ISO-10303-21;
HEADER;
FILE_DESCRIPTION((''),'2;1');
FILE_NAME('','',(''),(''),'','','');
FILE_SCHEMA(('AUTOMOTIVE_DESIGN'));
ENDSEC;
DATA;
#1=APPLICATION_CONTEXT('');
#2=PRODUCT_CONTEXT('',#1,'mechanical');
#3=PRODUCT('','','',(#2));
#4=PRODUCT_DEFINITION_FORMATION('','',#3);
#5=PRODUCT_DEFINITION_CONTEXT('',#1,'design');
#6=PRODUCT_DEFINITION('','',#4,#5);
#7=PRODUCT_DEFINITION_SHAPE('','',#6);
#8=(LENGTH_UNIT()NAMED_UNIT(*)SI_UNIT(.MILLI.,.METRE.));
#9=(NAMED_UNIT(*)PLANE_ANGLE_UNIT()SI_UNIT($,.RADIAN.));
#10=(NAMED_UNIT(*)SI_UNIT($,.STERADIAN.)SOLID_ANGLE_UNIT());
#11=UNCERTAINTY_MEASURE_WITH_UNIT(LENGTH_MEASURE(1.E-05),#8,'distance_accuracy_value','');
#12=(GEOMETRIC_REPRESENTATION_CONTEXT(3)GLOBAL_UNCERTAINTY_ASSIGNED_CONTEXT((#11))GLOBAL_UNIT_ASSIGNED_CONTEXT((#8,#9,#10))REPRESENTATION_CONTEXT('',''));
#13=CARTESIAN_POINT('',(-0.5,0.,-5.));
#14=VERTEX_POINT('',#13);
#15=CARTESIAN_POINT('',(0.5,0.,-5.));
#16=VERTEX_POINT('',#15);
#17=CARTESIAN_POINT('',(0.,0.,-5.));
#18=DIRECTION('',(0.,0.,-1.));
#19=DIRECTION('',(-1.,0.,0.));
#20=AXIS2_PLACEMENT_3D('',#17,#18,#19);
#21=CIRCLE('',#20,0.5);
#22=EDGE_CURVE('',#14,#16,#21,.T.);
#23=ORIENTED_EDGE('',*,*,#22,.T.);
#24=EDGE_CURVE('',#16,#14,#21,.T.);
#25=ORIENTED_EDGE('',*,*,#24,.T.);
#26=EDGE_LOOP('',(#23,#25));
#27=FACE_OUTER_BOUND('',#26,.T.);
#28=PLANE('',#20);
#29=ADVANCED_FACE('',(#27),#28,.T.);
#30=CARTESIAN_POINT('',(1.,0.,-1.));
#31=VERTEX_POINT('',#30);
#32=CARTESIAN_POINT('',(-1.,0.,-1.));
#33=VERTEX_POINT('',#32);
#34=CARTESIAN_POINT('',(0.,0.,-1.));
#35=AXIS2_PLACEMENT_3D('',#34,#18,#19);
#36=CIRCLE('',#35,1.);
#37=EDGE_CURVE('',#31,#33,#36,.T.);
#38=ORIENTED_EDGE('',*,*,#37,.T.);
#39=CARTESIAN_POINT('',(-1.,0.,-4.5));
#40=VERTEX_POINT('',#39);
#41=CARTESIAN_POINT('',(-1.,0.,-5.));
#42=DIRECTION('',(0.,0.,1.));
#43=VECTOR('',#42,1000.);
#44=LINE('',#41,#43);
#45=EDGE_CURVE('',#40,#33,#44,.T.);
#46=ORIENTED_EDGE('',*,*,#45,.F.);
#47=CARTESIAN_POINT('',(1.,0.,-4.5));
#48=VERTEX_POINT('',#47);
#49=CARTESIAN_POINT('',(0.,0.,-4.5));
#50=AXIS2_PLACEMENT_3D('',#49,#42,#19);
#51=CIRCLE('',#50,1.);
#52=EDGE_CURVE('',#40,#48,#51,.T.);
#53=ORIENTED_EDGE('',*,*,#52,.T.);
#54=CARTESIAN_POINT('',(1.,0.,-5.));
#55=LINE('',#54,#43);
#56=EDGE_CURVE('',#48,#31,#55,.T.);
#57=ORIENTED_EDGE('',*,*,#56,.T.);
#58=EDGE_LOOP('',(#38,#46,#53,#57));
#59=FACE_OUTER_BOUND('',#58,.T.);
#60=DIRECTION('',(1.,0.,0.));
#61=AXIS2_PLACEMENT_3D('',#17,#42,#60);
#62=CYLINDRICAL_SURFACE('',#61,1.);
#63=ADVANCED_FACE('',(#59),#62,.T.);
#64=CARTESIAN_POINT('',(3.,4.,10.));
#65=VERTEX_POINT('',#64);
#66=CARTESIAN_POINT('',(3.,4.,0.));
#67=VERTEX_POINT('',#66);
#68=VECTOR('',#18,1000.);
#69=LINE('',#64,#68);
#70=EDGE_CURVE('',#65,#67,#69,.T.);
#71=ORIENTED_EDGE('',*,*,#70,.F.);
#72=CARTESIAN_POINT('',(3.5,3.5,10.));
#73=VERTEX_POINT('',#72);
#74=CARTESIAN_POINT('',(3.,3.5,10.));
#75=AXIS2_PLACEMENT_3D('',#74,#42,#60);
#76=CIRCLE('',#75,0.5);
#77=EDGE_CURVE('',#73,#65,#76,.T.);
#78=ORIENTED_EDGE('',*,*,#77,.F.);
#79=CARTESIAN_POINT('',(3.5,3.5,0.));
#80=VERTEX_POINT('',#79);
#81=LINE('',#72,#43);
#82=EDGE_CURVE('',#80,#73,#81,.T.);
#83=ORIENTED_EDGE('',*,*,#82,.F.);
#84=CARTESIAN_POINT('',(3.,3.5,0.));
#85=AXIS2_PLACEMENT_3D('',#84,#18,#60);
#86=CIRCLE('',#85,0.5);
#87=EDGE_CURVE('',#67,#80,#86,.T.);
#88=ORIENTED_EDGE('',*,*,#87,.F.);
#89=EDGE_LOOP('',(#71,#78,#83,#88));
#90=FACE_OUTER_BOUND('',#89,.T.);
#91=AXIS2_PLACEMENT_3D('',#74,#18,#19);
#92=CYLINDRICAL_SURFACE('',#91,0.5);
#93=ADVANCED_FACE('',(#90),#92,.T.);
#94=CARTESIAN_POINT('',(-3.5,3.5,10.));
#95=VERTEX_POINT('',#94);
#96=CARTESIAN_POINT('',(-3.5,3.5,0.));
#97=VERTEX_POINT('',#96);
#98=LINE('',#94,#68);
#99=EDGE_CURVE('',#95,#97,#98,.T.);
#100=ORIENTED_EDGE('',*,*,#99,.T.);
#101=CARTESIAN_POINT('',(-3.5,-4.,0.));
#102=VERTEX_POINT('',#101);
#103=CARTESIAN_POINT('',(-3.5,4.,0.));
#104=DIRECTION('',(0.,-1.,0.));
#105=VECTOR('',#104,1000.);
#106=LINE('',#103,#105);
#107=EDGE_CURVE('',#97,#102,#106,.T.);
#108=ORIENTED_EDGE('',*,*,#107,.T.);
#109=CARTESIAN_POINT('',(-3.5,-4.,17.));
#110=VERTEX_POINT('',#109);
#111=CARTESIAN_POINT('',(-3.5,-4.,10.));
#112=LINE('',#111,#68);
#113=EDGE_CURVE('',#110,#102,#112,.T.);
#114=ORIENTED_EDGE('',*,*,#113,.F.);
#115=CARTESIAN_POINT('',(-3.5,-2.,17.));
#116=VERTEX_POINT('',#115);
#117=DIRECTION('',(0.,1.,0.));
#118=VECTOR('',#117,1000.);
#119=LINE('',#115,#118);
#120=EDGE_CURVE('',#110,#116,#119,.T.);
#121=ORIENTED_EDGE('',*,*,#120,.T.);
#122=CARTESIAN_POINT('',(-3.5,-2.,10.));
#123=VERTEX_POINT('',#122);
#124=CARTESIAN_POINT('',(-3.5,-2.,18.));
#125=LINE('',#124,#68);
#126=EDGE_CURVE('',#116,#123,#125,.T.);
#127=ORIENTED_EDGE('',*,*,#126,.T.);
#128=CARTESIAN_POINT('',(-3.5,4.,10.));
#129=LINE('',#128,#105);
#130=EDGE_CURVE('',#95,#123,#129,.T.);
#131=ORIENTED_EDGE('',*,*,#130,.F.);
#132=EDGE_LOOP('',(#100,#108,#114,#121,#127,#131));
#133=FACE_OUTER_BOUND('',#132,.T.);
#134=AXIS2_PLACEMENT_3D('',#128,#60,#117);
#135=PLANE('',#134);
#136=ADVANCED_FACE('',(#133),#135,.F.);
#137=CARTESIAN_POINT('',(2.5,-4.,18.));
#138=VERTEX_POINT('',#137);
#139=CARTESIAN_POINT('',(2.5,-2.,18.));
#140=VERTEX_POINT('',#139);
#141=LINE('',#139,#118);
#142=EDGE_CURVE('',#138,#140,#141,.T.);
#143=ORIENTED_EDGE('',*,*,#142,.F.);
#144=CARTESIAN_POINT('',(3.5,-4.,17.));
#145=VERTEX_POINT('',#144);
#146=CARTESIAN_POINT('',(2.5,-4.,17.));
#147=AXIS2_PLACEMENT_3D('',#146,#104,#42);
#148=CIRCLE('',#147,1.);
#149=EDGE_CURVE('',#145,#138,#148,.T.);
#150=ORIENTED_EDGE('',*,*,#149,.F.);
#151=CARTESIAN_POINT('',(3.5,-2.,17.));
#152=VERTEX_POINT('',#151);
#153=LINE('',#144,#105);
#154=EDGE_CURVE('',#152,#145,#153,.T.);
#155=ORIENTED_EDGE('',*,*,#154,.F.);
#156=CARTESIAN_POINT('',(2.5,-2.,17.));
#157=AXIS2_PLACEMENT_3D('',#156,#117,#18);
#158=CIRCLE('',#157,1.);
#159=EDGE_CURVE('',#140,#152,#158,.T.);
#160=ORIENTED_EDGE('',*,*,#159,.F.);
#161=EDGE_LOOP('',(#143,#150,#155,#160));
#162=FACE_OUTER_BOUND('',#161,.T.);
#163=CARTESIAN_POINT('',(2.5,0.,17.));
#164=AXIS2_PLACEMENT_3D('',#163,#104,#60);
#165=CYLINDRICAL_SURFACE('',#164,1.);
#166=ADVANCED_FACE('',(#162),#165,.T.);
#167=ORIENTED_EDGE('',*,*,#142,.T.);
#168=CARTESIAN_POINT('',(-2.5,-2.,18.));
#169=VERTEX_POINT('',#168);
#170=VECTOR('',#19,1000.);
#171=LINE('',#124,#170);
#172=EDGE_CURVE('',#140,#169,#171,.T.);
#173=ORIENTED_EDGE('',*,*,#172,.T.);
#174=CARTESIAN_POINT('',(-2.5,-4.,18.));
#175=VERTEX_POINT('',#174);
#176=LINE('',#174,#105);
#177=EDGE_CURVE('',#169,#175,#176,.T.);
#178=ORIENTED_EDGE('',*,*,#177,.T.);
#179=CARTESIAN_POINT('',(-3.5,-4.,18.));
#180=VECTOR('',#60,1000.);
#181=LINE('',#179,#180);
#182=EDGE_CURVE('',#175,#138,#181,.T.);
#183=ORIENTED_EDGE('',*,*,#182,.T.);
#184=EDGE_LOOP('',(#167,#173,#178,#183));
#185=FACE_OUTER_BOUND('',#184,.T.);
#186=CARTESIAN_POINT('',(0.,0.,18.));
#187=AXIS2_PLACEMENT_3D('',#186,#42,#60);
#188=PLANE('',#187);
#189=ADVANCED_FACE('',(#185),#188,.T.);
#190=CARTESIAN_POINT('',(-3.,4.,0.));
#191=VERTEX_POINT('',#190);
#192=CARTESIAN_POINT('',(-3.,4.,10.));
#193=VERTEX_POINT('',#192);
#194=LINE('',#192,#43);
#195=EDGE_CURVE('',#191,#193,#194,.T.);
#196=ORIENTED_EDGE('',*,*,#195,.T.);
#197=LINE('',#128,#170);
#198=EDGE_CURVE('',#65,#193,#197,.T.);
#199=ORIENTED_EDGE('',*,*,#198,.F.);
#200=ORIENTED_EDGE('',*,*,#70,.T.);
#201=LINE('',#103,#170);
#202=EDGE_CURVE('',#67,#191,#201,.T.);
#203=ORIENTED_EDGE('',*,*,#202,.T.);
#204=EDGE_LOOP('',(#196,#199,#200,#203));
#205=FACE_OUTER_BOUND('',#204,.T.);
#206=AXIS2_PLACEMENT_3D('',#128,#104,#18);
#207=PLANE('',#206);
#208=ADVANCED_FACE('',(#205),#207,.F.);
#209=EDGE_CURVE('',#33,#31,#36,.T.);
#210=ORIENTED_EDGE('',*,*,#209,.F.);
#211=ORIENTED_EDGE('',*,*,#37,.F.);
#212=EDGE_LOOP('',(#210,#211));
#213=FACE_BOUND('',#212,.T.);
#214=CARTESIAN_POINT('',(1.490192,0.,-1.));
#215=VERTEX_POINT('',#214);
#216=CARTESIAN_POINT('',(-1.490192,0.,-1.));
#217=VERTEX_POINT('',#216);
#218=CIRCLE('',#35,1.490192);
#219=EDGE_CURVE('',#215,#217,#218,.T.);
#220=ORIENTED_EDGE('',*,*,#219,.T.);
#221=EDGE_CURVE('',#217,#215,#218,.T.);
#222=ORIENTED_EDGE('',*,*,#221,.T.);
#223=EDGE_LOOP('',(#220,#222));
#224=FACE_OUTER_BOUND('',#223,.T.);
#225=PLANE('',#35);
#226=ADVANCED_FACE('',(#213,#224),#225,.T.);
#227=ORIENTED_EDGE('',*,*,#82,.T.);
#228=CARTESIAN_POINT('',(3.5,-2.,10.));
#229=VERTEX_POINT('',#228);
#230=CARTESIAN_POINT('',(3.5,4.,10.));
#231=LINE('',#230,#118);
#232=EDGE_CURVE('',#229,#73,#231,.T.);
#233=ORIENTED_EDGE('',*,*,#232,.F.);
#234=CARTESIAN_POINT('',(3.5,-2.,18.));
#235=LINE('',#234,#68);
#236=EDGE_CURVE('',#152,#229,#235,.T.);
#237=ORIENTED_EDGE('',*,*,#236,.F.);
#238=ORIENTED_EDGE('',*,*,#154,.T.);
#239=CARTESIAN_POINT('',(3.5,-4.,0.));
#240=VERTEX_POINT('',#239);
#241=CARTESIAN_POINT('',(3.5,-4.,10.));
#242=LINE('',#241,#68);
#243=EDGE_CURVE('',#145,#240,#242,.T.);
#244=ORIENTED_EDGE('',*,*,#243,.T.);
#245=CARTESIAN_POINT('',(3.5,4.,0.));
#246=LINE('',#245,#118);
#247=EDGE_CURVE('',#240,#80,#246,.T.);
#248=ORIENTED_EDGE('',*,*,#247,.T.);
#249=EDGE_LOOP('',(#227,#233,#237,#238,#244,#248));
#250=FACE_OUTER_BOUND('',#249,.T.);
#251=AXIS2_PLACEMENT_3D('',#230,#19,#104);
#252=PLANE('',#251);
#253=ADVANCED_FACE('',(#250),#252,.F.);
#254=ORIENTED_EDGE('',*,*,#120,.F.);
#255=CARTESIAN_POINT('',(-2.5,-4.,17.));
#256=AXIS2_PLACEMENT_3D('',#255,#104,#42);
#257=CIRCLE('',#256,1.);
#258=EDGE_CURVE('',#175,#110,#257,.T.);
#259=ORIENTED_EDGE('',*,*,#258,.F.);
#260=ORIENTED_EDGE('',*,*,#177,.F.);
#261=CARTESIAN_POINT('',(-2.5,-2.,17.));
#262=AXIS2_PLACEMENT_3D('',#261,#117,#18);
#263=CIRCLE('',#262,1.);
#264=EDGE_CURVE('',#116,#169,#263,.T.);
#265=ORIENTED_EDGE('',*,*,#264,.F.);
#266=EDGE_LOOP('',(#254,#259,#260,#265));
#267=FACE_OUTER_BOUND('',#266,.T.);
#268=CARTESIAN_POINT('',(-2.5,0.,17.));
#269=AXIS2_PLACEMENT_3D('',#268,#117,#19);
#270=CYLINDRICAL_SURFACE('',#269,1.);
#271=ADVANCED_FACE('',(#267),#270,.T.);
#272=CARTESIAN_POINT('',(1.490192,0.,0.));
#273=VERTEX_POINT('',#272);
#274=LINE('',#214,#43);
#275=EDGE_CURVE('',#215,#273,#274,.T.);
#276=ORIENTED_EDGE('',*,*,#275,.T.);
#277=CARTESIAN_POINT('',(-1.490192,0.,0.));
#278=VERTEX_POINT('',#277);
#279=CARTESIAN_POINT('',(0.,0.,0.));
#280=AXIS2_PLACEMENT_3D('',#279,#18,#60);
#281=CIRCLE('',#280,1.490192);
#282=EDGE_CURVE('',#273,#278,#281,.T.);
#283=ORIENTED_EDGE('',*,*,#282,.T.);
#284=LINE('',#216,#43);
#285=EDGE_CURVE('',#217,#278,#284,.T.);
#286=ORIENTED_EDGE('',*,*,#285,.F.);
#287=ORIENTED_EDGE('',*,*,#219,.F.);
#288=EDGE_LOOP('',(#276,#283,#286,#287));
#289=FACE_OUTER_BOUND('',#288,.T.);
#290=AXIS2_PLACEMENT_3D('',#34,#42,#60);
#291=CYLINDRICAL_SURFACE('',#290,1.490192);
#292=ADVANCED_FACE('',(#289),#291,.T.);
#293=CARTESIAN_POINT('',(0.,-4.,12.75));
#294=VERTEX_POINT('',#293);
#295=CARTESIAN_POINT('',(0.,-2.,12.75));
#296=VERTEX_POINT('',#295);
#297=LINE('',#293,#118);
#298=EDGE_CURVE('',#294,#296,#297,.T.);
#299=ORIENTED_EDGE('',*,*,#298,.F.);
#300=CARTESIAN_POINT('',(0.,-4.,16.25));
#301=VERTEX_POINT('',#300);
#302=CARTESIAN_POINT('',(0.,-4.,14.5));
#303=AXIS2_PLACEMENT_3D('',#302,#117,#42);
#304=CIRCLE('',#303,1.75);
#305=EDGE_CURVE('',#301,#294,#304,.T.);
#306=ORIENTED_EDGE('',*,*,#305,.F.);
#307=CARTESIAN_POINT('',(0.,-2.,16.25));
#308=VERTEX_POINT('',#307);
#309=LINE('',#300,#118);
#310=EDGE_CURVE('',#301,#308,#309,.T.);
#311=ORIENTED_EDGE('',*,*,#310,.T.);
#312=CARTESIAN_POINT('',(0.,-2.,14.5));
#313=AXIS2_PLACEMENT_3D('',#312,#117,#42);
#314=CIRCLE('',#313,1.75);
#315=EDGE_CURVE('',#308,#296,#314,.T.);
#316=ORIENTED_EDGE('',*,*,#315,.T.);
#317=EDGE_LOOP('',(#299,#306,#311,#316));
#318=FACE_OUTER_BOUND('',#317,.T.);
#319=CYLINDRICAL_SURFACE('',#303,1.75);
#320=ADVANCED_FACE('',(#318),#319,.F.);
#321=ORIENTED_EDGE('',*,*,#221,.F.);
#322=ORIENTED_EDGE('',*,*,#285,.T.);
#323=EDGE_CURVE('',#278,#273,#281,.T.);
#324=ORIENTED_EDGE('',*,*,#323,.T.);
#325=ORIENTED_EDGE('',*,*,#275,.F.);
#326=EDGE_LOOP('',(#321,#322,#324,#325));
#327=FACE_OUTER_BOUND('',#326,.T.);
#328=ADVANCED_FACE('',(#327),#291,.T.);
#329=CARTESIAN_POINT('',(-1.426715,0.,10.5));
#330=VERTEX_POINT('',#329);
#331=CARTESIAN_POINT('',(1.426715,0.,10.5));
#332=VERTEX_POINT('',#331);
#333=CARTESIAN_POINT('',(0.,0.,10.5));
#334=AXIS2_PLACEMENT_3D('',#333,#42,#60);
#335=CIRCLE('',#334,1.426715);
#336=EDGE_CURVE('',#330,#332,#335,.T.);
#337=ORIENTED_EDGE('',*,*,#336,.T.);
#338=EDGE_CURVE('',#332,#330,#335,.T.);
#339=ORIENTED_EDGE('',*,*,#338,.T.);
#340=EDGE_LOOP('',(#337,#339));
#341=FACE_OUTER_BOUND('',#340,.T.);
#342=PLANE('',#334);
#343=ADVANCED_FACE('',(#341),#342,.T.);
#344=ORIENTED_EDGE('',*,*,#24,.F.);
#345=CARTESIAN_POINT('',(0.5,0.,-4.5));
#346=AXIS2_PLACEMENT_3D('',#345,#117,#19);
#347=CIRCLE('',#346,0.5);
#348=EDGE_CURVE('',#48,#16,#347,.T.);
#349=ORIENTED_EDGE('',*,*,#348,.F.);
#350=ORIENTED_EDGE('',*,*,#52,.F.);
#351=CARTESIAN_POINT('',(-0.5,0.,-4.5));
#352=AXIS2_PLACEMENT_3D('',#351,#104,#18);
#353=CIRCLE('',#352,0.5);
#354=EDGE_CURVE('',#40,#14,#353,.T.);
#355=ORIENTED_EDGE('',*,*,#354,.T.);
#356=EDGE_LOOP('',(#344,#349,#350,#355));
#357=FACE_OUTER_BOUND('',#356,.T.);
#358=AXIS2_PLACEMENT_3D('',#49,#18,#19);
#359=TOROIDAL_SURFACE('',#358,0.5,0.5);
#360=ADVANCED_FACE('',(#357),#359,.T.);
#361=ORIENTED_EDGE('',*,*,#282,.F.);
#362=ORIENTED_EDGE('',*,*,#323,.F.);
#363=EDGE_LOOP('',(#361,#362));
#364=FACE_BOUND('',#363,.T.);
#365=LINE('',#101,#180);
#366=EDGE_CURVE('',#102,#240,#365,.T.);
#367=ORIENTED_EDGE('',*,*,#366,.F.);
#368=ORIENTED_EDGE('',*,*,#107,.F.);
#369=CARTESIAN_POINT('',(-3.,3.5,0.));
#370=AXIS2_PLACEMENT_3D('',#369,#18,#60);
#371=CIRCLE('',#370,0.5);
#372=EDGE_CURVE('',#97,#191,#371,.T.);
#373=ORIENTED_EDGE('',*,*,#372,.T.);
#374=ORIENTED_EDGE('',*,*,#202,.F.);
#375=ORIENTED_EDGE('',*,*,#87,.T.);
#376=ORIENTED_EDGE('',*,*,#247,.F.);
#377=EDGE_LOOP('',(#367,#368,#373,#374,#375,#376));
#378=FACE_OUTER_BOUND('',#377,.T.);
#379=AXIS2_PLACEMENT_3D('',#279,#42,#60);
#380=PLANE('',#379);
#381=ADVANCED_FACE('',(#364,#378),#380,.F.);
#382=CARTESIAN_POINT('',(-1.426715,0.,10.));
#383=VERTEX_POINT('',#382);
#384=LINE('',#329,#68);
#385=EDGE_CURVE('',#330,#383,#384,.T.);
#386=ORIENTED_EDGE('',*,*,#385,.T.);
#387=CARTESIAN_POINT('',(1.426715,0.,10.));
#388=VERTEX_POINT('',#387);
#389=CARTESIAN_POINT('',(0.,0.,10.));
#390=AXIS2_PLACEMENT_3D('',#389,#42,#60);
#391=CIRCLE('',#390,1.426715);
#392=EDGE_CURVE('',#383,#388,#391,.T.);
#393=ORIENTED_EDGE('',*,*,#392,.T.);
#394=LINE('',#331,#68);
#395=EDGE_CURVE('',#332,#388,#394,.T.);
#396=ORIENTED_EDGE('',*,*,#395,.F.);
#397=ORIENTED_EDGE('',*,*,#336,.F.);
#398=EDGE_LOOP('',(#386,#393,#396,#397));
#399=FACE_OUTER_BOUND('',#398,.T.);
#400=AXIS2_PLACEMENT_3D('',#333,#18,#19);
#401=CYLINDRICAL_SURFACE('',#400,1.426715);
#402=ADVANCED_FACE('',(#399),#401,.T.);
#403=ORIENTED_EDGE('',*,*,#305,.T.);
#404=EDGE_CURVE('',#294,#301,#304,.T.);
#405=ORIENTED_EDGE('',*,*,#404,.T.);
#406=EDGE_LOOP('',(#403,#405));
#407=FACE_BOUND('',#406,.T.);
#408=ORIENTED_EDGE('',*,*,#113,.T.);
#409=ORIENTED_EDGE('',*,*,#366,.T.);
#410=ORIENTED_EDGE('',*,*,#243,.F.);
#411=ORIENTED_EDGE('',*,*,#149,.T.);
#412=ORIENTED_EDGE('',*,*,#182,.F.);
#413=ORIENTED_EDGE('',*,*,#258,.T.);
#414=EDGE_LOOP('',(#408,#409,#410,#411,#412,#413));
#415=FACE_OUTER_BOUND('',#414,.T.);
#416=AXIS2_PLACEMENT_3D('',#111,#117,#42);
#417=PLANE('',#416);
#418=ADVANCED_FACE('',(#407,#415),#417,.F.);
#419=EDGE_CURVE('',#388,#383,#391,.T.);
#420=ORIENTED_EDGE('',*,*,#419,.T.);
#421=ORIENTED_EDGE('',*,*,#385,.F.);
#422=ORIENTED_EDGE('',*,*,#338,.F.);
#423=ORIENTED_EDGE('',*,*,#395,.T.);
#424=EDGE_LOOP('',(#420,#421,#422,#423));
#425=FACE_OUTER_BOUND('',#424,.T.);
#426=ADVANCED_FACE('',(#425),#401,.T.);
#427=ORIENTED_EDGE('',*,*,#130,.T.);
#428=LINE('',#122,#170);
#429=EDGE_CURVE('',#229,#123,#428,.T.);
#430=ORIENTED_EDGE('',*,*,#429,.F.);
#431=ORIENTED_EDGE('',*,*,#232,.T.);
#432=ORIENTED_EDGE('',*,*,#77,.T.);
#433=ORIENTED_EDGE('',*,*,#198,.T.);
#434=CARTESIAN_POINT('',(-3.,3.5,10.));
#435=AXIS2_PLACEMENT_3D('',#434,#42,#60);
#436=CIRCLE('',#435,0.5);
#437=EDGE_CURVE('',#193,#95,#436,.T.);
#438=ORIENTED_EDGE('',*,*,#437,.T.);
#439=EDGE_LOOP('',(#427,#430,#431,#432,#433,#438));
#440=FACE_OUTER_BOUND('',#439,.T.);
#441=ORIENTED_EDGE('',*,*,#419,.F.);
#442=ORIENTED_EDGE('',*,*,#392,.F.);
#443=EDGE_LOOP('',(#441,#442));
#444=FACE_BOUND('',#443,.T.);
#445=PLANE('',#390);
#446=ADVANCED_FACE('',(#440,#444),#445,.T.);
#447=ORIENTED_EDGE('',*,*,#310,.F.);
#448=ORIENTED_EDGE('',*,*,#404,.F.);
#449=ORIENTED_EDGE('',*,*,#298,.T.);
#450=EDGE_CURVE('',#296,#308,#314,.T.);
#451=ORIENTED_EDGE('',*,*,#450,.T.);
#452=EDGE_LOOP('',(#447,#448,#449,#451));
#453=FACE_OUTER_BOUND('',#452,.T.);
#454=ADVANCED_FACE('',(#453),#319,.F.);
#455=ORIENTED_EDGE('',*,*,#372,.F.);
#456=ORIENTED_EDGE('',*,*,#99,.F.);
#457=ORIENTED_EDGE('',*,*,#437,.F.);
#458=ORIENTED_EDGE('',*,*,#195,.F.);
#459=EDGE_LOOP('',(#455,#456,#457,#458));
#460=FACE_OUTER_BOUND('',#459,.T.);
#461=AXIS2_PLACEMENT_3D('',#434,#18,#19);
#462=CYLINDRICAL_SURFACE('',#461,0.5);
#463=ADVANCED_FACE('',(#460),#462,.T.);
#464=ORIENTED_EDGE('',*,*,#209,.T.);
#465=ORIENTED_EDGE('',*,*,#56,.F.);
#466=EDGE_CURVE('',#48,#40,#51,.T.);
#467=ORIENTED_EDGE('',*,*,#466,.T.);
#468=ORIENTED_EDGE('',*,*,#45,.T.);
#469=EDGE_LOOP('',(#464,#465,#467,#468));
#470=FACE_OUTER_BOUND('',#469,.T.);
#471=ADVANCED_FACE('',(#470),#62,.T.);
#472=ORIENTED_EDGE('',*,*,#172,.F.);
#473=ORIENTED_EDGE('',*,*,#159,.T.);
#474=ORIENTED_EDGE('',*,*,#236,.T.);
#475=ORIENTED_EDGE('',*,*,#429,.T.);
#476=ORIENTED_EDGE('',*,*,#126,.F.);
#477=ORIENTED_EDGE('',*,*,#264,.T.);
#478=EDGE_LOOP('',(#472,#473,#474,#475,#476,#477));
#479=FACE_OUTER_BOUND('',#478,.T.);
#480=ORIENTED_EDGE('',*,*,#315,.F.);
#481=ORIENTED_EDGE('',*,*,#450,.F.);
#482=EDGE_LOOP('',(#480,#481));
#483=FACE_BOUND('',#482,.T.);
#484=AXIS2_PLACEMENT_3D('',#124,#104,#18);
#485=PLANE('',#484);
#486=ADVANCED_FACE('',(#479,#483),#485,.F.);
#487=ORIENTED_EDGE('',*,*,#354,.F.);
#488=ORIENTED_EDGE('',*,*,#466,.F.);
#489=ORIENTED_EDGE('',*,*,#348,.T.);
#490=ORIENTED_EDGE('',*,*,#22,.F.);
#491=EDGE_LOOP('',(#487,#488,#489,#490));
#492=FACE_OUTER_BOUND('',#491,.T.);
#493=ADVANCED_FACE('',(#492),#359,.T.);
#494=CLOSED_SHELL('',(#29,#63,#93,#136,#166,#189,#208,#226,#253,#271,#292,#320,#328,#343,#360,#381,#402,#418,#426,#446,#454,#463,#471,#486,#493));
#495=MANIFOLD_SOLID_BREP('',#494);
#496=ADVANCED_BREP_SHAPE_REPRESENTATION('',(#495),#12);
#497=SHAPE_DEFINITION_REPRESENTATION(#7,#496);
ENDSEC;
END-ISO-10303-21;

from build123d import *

# Parameters (mm, degrees)
SKETCH1_W           = 7
SKETCH1_H           = 8
BOSS_EXTRUDE1_DEPTH = 10
SKETCH2_W           = 7
SKETCH2_H           = 2
BOSS_EXTRUDE2_DEPTH = 8
SKETCH3_R           = 1
BOSS_EXTRUDE3_DEPTH = 5
FILLET1_R           = 0.5
SKETCH4_R           = 1.490192279
BOSS_EXTRUDE4_DEPTH = 1
SKETCH5_R           = 1.426715447
BOSS_EXTRUDE5_DEPTH = 0.5
FILLET3_R           = 0.5
FILLET4_R           = 1
SKETCH6_R           = 1.75
CUT_EXTRUDE1_DEPTH  = 20.293781382


with BuildPart() as part:
    # Sketch1 → Boss-Extrude1 (new body)
    with BuildSketch(Plane.XY):
        Rectangle(SKETCH1_W, SKETCH1_H)
    extrude(amount=BOSS_EXTRUDE1_DEPTH)

    # Sketch2 → Boss-Extrude2 (add)
    with BuildSketch(Plane.XY.offset(10)):
        with Locations((0, -3)):
            Rectangle(SKETCH2_W, SKETCH2_H)
    extrude(amount=BOSS_EXTRUDE2_DEPTH)

    # Sketch3 → Boss-Extrude3 (add)
    with BuildSketch(Plane(origin=(0, 0, 0), x_dir=(-1, 0, 0), z_dir=(0, 0, -1))):
        Circle(SKETCH3_R)
    extrude(amount=BOSS_EXTRUDE3_DEPTH)

    # Fillet1
    fillet1_edges = [part.edges().sort_by_distance(p)[0] for p in [
        (1, 0, -5),
    ]]
    fillet(fillet1_edges, radius=FILLET1_R)

    # Sketch4 → Boss-Extrude4 (add)
    with BuildSketch(Plane(origin=(0, 0, 0), x_dir=(-1, 0, 0), z_dir=(0, 0, -1))):
        with Locations(Location((0, 0, 0), (0, 0, 180))):
            Circle(SKETCH4_R)
    extrude(amount=BOSS_EXTRUDE4_DEPTH)

    # Sketch5 → Boss-Extrude5 (add)
    with BuildSketch(Plane.XY.offset(10)):
        Circle(SKETCH5_R)
    extrude(amount=BOSS_EXTRUDE5_DEPTH)

    # Fillet3
    fillet3_edges = [part.edges().sort_by_distance(p)[0] for p in [
        (-3.5, 4, 5),
        (3.5, 4, 5),
    ]]
    fillet(fillet3_edges, radius=FILLET3_R)

    # Fillet4
    fillet4_edges = [part.edges().sort_by_distance(p)[0] for p in [
        (3.5, -3, 18),
        (-3.5, -3, 18),
    ]]
    fillet(fillet4_edges, radius=FILLET4_R)

    # Sketch6 → Cut-Extrude1 (cut, through all)
    with BuildSketch(Plane(origin=(0, -2, 0), x_dir=(1, 0, 0), z_dir=(0, 1, 0))):
        with Locations(Location((0, -14.5, 0), (0, 0, 270))):
            Circle(SKETCH6_R)
    extrude(amount=-CUT_EXTRUDE1_DEPTH, mode=Mode.SUBTRACT)


solid = part.part
